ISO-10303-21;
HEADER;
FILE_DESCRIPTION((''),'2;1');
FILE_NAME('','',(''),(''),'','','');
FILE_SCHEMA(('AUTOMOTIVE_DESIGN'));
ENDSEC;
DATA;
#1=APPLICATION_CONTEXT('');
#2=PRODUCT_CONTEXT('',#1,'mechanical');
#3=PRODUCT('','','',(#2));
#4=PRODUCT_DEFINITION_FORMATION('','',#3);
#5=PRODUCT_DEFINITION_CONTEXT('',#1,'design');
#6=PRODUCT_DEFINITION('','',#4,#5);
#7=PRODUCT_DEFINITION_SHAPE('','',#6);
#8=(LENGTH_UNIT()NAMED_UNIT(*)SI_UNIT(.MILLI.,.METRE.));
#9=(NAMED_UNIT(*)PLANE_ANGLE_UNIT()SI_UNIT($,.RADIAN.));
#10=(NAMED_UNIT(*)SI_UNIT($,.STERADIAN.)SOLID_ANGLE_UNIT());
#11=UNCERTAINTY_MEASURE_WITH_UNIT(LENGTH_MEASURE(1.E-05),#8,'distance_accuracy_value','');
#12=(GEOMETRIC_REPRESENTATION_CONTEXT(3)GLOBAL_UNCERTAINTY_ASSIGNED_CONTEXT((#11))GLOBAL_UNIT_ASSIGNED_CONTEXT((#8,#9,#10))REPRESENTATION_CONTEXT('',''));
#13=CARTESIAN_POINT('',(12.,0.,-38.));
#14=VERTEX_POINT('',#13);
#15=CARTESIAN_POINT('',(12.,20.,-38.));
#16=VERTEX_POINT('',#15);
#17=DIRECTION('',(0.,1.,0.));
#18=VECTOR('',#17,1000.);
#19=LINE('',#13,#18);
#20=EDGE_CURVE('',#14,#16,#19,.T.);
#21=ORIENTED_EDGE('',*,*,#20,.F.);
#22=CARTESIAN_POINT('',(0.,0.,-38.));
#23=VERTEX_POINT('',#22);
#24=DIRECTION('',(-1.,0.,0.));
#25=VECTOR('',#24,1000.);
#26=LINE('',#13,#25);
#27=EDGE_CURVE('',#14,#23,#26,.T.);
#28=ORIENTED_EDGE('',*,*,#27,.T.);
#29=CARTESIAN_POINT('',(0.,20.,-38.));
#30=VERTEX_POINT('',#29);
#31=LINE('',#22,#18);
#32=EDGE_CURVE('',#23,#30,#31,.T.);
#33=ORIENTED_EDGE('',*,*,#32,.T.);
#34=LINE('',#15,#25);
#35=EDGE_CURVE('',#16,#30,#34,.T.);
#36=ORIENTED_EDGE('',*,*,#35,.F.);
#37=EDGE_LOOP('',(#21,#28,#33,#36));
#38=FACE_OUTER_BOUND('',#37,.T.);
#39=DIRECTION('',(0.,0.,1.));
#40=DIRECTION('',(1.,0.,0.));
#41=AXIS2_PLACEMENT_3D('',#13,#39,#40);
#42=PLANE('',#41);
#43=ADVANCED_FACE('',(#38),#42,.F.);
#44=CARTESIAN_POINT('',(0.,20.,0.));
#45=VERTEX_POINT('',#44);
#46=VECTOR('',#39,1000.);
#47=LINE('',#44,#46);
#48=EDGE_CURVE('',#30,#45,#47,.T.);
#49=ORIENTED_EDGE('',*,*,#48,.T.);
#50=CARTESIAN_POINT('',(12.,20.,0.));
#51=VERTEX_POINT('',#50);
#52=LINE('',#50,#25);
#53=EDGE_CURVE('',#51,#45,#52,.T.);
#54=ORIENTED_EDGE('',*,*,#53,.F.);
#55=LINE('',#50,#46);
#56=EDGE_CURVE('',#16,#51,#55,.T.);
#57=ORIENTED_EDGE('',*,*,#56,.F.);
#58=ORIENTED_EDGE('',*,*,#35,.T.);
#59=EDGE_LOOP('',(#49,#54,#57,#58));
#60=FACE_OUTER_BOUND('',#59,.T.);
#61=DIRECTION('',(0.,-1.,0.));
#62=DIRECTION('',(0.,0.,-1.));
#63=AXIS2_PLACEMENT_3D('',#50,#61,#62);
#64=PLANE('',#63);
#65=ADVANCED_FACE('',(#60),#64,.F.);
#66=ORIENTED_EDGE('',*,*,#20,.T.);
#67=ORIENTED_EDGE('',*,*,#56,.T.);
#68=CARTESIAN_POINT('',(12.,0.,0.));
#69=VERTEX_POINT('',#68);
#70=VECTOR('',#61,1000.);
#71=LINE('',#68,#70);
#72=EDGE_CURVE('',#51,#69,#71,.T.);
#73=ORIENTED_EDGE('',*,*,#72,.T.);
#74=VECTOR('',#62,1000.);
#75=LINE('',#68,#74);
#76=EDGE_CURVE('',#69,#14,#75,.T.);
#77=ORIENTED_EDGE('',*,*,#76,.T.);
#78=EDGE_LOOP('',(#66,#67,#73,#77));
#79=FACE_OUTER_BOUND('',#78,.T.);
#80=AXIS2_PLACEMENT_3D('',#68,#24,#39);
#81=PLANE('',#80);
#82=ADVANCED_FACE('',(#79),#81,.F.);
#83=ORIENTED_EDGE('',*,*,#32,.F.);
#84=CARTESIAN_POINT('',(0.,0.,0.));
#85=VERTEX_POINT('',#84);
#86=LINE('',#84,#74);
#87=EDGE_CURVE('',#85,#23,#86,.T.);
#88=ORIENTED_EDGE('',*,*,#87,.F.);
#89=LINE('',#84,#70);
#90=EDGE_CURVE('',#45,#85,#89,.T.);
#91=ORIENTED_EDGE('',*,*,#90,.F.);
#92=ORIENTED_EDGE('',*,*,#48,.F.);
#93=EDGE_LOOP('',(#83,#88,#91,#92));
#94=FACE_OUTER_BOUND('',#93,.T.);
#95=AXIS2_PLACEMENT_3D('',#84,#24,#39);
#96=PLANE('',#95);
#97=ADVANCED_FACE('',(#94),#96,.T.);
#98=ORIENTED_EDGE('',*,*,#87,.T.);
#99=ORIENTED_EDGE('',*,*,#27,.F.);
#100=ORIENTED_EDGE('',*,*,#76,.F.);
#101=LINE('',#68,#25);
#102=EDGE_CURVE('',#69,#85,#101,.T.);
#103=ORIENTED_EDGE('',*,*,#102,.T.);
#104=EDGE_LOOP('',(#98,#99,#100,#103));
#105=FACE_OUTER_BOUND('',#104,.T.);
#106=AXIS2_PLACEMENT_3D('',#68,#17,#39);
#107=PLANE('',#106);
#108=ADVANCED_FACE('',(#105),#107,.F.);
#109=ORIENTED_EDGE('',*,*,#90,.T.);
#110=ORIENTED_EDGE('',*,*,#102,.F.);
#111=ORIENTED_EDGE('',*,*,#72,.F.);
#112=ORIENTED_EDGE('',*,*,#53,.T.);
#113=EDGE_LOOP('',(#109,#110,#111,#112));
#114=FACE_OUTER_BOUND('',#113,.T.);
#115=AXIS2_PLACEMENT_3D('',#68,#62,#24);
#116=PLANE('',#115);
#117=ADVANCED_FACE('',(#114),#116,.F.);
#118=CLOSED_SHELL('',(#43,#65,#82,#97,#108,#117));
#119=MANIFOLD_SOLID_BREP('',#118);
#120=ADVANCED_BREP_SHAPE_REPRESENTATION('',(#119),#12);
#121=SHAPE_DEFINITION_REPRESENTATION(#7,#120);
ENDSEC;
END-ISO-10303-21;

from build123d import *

# Parameters (mm, degrees)
SKETCH1_W           = 38
SKETCH1_H           = 20
BOSS_EXTRUDE1_DEPTH = 12


with BuildPart() as part:
    # Sketch1 → Boss-Extrude1 (new body)
    with BuildSketch(Plane(origin=(0, 0, 0), x_dir=(0, 0, -1), z_dir=(1, 0, 0))):
        with Locations((19, 10)):
            Rectangle(SKETCH1_W, SKETCH1_H)
    extrude(amount=BOSS_EXTRUDE1_DEPTH)


solid = part.part
